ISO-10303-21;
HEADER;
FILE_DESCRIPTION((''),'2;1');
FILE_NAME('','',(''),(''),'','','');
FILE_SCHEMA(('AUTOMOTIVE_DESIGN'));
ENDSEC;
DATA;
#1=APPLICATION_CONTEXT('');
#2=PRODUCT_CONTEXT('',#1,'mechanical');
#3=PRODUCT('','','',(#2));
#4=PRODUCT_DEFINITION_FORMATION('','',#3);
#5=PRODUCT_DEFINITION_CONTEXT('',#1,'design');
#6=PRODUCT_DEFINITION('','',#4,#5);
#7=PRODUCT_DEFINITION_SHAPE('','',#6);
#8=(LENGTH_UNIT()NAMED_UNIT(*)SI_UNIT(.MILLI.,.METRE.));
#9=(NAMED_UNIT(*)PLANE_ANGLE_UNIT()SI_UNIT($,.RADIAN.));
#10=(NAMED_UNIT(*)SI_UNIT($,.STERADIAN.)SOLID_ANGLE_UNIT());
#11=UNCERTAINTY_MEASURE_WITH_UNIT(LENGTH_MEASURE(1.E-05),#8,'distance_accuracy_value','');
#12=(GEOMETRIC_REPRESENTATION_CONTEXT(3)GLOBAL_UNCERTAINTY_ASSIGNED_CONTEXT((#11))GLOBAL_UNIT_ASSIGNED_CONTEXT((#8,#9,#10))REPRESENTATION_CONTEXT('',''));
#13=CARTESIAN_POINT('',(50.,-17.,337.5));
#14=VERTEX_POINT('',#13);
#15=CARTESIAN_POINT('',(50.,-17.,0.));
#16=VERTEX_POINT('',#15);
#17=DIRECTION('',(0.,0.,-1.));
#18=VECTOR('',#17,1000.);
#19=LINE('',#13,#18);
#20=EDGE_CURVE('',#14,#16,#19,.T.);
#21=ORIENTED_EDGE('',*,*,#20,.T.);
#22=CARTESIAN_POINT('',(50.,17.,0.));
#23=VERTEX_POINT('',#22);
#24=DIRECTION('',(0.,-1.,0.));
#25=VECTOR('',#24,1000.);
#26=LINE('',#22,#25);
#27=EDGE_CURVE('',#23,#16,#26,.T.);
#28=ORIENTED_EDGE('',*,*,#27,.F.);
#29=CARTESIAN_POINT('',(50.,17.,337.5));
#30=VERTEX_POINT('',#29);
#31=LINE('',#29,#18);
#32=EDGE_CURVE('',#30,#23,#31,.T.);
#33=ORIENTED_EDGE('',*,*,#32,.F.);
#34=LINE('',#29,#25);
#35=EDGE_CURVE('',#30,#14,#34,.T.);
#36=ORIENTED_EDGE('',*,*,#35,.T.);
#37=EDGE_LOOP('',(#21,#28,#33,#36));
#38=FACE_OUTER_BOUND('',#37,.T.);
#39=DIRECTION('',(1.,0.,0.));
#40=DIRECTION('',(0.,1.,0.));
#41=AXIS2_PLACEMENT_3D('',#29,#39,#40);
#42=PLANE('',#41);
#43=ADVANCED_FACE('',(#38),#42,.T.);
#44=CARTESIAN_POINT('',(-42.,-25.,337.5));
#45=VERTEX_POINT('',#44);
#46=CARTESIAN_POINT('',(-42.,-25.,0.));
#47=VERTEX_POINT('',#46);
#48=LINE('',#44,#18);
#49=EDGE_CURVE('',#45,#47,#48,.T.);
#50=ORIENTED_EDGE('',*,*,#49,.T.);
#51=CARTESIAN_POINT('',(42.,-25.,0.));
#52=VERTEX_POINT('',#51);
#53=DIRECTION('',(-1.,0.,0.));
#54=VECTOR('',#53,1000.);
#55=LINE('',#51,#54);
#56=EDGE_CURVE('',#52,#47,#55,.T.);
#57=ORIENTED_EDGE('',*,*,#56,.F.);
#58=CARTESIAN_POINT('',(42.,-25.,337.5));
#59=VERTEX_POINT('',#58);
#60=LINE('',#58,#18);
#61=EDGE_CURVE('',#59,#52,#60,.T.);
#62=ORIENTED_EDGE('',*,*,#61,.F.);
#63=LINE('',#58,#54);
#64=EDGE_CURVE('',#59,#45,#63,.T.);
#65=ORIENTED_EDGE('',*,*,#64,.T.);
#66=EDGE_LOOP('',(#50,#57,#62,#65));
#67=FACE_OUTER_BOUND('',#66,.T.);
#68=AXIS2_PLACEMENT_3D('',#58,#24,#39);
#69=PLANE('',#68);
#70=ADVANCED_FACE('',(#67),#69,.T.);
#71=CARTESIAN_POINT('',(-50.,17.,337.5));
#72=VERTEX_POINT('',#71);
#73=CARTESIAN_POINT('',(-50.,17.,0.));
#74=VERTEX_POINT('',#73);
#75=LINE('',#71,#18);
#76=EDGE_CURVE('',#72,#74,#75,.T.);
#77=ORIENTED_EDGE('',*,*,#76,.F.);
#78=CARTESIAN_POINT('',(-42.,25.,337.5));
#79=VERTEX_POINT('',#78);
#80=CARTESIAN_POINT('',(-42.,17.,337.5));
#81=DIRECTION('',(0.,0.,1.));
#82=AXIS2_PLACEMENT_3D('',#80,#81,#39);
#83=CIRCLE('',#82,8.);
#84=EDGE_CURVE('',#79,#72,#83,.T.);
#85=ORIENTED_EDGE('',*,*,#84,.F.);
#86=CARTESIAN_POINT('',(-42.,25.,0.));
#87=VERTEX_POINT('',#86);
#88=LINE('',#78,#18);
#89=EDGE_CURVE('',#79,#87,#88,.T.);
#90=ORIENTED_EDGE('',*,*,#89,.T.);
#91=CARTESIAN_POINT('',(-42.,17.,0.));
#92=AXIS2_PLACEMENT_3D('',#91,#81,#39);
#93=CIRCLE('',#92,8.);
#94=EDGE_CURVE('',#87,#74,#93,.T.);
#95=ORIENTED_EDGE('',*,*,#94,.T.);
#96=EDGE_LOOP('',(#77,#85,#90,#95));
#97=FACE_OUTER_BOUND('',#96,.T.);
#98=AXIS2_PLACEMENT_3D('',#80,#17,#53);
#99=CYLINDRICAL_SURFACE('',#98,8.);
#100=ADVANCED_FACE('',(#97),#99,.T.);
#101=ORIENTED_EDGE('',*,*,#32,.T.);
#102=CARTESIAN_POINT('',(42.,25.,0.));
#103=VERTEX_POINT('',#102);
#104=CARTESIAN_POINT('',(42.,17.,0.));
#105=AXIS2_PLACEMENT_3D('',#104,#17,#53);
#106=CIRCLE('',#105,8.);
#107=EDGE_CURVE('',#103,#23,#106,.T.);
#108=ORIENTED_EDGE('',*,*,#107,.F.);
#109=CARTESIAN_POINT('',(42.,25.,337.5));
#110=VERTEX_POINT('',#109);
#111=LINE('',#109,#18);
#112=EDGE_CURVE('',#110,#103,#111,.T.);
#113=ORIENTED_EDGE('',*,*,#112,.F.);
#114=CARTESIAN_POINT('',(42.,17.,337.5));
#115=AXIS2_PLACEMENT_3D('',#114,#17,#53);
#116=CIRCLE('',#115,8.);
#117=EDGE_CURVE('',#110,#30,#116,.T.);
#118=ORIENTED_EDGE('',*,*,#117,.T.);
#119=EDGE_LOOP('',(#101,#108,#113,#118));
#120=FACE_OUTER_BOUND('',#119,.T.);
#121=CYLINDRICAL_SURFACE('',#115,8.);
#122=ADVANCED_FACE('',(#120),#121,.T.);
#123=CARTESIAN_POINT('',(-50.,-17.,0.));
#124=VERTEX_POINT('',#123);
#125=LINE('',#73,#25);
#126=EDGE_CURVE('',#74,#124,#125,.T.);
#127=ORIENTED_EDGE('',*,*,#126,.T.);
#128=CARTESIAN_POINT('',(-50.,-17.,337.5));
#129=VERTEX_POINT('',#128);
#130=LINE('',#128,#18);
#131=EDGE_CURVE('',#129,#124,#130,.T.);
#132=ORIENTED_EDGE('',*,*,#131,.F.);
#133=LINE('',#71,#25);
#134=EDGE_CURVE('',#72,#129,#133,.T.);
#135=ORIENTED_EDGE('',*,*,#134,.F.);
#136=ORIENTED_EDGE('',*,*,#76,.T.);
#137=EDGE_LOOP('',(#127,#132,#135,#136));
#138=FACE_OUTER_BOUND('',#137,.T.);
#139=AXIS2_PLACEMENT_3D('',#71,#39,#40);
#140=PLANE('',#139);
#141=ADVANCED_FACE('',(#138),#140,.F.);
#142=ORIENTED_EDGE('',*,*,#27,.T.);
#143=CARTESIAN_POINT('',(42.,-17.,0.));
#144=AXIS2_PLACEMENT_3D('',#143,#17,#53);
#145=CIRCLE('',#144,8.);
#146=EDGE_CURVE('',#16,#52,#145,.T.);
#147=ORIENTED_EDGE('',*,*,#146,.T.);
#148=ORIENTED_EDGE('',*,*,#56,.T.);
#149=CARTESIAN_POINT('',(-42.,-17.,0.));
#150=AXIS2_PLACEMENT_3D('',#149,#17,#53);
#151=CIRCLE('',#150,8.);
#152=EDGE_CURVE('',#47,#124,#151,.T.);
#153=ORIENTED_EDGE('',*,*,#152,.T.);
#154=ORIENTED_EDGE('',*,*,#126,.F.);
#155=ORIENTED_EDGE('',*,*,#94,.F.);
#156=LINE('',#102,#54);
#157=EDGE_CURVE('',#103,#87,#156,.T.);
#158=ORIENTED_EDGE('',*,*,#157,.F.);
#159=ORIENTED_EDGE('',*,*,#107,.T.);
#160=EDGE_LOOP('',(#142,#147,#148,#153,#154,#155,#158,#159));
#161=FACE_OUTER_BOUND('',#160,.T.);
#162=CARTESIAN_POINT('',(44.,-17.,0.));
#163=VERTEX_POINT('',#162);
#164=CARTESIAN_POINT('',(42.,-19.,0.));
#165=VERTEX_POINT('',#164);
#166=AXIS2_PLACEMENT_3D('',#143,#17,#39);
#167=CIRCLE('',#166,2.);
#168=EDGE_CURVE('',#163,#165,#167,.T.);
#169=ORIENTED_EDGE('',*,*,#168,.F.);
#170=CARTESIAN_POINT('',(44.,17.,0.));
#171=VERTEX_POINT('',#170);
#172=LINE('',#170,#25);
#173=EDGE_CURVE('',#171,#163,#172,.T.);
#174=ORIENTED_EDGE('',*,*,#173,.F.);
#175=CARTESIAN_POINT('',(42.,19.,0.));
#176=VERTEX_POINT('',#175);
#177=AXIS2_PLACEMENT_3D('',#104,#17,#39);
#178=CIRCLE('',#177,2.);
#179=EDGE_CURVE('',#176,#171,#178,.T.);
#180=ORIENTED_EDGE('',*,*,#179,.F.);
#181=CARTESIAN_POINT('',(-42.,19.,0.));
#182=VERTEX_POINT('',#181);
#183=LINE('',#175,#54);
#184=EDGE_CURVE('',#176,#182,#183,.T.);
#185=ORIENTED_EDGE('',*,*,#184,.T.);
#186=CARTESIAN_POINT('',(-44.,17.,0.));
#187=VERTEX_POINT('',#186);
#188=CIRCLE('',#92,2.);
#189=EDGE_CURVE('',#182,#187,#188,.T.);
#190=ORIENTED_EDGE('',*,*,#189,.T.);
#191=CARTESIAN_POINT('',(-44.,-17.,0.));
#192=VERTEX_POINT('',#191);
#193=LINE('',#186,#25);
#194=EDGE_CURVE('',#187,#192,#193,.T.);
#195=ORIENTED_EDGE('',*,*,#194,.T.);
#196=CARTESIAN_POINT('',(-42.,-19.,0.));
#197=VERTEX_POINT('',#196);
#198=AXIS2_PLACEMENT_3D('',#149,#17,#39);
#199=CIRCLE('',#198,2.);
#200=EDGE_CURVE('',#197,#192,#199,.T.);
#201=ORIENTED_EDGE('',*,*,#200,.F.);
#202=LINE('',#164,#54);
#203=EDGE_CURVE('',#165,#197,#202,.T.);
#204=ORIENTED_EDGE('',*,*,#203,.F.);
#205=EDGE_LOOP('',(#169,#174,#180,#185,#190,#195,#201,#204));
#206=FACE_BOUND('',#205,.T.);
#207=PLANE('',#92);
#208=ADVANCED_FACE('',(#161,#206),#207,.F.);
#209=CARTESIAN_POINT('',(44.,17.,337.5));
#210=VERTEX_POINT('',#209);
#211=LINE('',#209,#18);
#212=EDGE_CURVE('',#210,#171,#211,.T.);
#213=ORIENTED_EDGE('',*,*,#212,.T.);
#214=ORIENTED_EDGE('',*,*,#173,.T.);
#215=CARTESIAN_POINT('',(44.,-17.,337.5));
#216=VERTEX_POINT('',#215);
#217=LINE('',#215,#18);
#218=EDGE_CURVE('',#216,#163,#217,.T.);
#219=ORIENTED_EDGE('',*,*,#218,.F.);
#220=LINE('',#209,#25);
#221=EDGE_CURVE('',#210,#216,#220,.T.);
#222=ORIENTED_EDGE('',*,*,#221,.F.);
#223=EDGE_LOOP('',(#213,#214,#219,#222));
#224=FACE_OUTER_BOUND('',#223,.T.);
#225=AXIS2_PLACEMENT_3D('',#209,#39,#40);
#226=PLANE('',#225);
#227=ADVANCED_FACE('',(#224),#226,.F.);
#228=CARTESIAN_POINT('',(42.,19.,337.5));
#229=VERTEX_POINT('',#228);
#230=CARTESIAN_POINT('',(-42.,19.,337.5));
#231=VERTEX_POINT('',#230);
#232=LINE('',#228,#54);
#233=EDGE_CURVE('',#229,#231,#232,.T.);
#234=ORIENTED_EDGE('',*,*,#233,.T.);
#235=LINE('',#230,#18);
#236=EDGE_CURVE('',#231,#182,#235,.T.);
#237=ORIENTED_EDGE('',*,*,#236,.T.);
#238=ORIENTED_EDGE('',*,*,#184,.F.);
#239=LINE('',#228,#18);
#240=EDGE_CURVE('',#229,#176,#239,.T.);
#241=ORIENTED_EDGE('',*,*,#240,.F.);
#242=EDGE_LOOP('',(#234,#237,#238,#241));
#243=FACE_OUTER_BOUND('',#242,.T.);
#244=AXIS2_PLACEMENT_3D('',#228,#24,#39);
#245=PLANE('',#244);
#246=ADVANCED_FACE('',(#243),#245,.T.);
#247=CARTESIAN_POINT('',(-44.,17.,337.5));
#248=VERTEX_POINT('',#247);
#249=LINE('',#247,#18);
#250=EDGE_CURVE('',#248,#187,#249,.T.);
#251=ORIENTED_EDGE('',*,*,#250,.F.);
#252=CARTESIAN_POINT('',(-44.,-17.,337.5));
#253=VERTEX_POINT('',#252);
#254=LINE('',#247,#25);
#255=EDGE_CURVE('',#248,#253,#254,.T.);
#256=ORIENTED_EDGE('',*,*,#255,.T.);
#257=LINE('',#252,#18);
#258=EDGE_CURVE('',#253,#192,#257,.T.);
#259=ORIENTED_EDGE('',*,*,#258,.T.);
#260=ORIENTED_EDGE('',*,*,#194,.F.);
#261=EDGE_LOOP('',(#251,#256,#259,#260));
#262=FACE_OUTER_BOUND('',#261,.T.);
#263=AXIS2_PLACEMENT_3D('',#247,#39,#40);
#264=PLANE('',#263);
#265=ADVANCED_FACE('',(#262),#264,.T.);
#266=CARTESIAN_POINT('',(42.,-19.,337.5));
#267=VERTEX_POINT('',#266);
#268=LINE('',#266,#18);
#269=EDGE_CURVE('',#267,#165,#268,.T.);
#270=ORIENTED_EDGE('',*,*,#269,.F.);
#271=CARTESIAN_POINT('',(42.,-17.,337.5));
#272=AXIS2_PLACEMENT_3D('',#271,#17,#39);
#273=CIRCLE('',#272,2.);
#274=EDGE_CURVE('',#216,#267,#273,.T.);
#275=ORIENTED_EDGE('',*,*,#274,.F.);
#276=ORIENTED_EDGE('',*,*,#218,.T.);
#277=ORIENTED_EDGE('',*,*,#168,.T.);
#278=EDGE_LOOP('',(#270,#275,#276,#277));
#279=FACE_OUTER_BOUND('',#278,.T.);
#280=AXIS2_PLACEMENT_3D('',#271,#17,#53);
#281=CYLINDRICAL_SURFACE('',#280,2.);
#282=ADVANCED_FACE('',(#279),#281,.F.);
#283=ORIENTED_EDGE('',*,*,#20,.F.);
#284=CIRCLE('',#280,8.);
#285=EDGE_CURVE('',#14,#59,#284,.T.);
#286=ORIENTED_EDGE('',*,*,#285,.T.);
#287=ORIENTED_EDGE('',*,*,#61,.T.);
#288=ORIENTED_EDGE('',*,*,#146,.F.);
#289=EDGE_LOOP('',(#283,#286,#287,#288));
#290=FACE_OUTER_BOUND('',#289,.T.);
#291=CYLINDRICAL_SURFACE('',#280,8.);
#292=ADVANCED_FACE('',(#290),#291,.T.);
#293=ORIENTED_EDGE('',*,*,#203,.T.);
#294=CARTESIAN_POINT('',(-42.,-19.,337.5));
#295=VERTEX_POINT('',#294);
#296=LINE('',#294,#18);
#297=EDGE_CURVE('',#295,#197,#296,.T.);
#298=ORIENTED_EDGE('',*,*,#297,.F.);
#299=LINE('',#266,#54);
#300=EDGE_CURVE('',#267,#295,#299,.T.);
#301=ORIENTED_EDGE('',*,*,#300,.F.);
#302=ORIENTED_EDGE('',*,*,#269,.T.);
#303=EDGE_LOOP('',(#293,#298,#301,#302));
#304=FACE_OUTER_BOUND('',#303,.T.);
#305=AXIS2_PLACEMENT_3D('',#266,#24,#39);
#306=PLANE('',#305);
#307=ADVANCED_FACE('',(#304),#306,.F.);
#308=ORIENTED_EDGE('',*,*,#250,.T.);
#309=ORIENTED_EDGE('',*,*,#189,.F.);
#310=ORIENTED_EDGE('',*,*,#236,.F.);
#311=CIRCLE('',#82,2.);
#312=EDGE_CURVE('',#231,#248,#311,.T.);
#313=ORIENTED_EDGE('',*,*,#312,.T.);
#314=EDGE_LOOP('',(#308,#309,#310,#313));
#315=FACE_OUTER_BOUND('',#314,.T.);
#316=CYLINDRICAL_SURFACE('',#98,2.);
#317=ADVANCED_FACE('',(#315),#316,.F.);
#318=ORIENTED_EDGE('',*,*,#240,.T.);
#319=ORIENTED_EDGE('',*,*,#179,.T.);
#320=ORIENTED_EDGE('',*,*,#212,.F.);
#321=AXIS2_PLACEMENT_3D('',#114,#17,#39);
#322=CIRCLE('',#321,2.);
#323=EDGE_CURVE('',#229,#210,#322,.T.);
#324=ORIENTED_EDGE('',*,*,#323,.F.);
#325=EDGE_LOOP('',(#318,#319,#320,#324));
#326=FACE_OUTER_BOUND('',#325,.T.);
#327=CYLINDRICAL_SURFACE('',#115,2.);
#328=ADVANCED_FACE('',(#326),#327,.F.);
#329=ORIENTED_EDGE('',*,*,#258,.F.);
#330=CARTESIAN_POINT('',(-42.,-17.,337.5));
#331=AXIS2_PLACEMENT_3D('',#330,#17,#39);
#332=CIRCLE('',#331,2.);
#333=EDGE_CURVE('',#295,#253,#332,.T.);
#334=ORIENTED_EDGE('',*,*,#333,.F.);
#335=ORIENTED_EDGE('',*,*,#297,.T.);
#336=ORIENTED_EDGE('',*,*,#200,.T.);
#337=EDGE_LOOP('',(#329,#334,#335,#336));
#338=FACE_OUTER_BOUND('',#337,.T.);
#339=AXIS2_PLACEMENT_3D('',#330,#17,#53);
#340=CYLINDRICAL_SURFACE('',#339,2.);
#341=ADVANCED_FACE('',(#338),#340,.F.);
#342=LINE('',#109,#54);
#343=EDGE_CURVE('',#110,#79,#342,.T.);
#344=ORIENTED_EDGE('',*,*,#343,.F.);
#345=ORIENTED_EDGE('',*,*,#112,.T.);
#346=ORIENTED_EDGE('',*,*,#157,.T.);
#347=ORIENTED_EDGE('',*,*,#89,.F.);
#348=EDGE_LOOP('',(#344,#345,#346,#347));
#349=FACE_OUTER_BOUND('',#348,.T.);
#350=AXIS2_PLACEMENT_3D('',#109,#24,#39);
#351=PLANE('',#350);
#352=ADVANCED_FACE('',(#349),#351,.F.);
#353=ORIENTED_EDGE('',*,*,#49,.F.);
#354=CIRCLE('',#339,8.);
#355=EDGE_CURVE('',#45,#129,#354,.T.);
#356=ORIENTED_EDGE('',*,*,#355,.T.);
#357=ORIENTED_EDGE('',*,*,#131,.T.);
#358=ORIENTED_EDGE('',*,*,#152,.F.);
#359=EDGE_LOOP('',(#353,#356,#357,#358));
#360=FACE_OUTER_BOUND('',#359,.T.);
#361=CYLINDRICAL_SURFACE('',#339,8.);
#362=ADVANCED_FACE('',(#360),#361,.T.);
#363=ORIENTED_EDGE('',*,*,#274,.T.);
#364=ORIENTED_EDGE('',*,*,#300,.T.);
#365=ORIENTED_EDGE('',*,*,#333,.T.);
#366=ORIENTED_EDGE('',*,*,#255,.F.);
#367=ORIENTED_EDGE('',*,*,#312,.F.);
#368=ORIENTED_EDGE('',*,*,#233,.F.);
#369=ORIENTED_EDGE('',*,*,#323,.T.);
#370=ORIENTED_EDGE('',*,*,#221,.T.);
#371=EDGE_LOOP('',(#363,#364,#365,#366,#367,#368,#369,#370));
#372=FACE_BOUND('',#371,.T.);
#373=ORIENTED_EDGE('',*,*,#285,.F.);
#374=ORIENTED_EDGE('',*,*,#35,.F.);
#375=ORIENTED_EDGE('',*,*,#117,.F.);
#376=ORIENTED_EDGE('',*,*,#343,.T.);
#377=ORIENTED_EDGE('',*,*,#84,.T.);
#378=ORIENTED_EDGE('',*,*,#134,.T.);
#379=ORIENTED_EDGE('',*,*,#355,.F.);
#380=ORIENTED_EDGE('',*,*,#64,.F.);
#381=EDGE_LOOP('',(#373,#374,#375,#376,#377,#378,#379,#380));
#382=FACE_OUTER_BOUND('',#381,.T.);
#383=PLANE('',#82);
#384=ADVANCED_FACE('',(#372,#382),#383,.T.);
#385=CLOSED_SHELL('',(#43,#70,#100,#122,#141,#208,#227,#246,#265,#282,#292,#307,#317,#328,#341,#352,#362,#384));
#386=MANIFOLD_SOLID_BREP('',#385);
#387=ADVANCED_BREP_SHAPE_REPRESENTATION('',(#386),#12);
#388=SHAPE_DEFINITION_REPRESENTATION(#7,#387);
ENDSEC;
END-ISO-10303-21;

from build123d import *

# Parameters (mm, degrees)
BOSS_EXTRUDE2_DEPTH = 337.5
SHELL1_T            = -6


with BuildPart() as part:
    # Sketch2 → Boss-Extrude2 (new body)
    with BuildSketch(Plane.XY):
        with BuildLine():
            Line((42, 25), (-42, 25))
            ThreePointArc((-42, 25), (-47.656854249, 22.656854249), (-50, 17))
            Line((-50, 17), (-50, -17))
            ThreePointArc((-50, -17), (-47.656854249, -22.656854249), (-42, -25))
            Line((-42, -25), (42, -25))
            ThreePointArc((42, -25), (47.656854249, -22.656854249), (50, -17))
            Line((50, -17), (50, 17))
            ThreePointArc((50, 17), (47.656854249, 22.656854249), (42, 25))
        make_face()
    extrude(amount=BOSS_EXTRUDE2_DEPTH)

    # Shell1
    shell1_openings = [part.faces().sort_by_distance(p)[0] for p in [
        (0, 0, 337.5),
        (0, 0, 0),
    ]]
    offset(amount=SHELL1_T, openings=shell1_openings, kind=Kind.INTERSECTION)


solid = part.part
